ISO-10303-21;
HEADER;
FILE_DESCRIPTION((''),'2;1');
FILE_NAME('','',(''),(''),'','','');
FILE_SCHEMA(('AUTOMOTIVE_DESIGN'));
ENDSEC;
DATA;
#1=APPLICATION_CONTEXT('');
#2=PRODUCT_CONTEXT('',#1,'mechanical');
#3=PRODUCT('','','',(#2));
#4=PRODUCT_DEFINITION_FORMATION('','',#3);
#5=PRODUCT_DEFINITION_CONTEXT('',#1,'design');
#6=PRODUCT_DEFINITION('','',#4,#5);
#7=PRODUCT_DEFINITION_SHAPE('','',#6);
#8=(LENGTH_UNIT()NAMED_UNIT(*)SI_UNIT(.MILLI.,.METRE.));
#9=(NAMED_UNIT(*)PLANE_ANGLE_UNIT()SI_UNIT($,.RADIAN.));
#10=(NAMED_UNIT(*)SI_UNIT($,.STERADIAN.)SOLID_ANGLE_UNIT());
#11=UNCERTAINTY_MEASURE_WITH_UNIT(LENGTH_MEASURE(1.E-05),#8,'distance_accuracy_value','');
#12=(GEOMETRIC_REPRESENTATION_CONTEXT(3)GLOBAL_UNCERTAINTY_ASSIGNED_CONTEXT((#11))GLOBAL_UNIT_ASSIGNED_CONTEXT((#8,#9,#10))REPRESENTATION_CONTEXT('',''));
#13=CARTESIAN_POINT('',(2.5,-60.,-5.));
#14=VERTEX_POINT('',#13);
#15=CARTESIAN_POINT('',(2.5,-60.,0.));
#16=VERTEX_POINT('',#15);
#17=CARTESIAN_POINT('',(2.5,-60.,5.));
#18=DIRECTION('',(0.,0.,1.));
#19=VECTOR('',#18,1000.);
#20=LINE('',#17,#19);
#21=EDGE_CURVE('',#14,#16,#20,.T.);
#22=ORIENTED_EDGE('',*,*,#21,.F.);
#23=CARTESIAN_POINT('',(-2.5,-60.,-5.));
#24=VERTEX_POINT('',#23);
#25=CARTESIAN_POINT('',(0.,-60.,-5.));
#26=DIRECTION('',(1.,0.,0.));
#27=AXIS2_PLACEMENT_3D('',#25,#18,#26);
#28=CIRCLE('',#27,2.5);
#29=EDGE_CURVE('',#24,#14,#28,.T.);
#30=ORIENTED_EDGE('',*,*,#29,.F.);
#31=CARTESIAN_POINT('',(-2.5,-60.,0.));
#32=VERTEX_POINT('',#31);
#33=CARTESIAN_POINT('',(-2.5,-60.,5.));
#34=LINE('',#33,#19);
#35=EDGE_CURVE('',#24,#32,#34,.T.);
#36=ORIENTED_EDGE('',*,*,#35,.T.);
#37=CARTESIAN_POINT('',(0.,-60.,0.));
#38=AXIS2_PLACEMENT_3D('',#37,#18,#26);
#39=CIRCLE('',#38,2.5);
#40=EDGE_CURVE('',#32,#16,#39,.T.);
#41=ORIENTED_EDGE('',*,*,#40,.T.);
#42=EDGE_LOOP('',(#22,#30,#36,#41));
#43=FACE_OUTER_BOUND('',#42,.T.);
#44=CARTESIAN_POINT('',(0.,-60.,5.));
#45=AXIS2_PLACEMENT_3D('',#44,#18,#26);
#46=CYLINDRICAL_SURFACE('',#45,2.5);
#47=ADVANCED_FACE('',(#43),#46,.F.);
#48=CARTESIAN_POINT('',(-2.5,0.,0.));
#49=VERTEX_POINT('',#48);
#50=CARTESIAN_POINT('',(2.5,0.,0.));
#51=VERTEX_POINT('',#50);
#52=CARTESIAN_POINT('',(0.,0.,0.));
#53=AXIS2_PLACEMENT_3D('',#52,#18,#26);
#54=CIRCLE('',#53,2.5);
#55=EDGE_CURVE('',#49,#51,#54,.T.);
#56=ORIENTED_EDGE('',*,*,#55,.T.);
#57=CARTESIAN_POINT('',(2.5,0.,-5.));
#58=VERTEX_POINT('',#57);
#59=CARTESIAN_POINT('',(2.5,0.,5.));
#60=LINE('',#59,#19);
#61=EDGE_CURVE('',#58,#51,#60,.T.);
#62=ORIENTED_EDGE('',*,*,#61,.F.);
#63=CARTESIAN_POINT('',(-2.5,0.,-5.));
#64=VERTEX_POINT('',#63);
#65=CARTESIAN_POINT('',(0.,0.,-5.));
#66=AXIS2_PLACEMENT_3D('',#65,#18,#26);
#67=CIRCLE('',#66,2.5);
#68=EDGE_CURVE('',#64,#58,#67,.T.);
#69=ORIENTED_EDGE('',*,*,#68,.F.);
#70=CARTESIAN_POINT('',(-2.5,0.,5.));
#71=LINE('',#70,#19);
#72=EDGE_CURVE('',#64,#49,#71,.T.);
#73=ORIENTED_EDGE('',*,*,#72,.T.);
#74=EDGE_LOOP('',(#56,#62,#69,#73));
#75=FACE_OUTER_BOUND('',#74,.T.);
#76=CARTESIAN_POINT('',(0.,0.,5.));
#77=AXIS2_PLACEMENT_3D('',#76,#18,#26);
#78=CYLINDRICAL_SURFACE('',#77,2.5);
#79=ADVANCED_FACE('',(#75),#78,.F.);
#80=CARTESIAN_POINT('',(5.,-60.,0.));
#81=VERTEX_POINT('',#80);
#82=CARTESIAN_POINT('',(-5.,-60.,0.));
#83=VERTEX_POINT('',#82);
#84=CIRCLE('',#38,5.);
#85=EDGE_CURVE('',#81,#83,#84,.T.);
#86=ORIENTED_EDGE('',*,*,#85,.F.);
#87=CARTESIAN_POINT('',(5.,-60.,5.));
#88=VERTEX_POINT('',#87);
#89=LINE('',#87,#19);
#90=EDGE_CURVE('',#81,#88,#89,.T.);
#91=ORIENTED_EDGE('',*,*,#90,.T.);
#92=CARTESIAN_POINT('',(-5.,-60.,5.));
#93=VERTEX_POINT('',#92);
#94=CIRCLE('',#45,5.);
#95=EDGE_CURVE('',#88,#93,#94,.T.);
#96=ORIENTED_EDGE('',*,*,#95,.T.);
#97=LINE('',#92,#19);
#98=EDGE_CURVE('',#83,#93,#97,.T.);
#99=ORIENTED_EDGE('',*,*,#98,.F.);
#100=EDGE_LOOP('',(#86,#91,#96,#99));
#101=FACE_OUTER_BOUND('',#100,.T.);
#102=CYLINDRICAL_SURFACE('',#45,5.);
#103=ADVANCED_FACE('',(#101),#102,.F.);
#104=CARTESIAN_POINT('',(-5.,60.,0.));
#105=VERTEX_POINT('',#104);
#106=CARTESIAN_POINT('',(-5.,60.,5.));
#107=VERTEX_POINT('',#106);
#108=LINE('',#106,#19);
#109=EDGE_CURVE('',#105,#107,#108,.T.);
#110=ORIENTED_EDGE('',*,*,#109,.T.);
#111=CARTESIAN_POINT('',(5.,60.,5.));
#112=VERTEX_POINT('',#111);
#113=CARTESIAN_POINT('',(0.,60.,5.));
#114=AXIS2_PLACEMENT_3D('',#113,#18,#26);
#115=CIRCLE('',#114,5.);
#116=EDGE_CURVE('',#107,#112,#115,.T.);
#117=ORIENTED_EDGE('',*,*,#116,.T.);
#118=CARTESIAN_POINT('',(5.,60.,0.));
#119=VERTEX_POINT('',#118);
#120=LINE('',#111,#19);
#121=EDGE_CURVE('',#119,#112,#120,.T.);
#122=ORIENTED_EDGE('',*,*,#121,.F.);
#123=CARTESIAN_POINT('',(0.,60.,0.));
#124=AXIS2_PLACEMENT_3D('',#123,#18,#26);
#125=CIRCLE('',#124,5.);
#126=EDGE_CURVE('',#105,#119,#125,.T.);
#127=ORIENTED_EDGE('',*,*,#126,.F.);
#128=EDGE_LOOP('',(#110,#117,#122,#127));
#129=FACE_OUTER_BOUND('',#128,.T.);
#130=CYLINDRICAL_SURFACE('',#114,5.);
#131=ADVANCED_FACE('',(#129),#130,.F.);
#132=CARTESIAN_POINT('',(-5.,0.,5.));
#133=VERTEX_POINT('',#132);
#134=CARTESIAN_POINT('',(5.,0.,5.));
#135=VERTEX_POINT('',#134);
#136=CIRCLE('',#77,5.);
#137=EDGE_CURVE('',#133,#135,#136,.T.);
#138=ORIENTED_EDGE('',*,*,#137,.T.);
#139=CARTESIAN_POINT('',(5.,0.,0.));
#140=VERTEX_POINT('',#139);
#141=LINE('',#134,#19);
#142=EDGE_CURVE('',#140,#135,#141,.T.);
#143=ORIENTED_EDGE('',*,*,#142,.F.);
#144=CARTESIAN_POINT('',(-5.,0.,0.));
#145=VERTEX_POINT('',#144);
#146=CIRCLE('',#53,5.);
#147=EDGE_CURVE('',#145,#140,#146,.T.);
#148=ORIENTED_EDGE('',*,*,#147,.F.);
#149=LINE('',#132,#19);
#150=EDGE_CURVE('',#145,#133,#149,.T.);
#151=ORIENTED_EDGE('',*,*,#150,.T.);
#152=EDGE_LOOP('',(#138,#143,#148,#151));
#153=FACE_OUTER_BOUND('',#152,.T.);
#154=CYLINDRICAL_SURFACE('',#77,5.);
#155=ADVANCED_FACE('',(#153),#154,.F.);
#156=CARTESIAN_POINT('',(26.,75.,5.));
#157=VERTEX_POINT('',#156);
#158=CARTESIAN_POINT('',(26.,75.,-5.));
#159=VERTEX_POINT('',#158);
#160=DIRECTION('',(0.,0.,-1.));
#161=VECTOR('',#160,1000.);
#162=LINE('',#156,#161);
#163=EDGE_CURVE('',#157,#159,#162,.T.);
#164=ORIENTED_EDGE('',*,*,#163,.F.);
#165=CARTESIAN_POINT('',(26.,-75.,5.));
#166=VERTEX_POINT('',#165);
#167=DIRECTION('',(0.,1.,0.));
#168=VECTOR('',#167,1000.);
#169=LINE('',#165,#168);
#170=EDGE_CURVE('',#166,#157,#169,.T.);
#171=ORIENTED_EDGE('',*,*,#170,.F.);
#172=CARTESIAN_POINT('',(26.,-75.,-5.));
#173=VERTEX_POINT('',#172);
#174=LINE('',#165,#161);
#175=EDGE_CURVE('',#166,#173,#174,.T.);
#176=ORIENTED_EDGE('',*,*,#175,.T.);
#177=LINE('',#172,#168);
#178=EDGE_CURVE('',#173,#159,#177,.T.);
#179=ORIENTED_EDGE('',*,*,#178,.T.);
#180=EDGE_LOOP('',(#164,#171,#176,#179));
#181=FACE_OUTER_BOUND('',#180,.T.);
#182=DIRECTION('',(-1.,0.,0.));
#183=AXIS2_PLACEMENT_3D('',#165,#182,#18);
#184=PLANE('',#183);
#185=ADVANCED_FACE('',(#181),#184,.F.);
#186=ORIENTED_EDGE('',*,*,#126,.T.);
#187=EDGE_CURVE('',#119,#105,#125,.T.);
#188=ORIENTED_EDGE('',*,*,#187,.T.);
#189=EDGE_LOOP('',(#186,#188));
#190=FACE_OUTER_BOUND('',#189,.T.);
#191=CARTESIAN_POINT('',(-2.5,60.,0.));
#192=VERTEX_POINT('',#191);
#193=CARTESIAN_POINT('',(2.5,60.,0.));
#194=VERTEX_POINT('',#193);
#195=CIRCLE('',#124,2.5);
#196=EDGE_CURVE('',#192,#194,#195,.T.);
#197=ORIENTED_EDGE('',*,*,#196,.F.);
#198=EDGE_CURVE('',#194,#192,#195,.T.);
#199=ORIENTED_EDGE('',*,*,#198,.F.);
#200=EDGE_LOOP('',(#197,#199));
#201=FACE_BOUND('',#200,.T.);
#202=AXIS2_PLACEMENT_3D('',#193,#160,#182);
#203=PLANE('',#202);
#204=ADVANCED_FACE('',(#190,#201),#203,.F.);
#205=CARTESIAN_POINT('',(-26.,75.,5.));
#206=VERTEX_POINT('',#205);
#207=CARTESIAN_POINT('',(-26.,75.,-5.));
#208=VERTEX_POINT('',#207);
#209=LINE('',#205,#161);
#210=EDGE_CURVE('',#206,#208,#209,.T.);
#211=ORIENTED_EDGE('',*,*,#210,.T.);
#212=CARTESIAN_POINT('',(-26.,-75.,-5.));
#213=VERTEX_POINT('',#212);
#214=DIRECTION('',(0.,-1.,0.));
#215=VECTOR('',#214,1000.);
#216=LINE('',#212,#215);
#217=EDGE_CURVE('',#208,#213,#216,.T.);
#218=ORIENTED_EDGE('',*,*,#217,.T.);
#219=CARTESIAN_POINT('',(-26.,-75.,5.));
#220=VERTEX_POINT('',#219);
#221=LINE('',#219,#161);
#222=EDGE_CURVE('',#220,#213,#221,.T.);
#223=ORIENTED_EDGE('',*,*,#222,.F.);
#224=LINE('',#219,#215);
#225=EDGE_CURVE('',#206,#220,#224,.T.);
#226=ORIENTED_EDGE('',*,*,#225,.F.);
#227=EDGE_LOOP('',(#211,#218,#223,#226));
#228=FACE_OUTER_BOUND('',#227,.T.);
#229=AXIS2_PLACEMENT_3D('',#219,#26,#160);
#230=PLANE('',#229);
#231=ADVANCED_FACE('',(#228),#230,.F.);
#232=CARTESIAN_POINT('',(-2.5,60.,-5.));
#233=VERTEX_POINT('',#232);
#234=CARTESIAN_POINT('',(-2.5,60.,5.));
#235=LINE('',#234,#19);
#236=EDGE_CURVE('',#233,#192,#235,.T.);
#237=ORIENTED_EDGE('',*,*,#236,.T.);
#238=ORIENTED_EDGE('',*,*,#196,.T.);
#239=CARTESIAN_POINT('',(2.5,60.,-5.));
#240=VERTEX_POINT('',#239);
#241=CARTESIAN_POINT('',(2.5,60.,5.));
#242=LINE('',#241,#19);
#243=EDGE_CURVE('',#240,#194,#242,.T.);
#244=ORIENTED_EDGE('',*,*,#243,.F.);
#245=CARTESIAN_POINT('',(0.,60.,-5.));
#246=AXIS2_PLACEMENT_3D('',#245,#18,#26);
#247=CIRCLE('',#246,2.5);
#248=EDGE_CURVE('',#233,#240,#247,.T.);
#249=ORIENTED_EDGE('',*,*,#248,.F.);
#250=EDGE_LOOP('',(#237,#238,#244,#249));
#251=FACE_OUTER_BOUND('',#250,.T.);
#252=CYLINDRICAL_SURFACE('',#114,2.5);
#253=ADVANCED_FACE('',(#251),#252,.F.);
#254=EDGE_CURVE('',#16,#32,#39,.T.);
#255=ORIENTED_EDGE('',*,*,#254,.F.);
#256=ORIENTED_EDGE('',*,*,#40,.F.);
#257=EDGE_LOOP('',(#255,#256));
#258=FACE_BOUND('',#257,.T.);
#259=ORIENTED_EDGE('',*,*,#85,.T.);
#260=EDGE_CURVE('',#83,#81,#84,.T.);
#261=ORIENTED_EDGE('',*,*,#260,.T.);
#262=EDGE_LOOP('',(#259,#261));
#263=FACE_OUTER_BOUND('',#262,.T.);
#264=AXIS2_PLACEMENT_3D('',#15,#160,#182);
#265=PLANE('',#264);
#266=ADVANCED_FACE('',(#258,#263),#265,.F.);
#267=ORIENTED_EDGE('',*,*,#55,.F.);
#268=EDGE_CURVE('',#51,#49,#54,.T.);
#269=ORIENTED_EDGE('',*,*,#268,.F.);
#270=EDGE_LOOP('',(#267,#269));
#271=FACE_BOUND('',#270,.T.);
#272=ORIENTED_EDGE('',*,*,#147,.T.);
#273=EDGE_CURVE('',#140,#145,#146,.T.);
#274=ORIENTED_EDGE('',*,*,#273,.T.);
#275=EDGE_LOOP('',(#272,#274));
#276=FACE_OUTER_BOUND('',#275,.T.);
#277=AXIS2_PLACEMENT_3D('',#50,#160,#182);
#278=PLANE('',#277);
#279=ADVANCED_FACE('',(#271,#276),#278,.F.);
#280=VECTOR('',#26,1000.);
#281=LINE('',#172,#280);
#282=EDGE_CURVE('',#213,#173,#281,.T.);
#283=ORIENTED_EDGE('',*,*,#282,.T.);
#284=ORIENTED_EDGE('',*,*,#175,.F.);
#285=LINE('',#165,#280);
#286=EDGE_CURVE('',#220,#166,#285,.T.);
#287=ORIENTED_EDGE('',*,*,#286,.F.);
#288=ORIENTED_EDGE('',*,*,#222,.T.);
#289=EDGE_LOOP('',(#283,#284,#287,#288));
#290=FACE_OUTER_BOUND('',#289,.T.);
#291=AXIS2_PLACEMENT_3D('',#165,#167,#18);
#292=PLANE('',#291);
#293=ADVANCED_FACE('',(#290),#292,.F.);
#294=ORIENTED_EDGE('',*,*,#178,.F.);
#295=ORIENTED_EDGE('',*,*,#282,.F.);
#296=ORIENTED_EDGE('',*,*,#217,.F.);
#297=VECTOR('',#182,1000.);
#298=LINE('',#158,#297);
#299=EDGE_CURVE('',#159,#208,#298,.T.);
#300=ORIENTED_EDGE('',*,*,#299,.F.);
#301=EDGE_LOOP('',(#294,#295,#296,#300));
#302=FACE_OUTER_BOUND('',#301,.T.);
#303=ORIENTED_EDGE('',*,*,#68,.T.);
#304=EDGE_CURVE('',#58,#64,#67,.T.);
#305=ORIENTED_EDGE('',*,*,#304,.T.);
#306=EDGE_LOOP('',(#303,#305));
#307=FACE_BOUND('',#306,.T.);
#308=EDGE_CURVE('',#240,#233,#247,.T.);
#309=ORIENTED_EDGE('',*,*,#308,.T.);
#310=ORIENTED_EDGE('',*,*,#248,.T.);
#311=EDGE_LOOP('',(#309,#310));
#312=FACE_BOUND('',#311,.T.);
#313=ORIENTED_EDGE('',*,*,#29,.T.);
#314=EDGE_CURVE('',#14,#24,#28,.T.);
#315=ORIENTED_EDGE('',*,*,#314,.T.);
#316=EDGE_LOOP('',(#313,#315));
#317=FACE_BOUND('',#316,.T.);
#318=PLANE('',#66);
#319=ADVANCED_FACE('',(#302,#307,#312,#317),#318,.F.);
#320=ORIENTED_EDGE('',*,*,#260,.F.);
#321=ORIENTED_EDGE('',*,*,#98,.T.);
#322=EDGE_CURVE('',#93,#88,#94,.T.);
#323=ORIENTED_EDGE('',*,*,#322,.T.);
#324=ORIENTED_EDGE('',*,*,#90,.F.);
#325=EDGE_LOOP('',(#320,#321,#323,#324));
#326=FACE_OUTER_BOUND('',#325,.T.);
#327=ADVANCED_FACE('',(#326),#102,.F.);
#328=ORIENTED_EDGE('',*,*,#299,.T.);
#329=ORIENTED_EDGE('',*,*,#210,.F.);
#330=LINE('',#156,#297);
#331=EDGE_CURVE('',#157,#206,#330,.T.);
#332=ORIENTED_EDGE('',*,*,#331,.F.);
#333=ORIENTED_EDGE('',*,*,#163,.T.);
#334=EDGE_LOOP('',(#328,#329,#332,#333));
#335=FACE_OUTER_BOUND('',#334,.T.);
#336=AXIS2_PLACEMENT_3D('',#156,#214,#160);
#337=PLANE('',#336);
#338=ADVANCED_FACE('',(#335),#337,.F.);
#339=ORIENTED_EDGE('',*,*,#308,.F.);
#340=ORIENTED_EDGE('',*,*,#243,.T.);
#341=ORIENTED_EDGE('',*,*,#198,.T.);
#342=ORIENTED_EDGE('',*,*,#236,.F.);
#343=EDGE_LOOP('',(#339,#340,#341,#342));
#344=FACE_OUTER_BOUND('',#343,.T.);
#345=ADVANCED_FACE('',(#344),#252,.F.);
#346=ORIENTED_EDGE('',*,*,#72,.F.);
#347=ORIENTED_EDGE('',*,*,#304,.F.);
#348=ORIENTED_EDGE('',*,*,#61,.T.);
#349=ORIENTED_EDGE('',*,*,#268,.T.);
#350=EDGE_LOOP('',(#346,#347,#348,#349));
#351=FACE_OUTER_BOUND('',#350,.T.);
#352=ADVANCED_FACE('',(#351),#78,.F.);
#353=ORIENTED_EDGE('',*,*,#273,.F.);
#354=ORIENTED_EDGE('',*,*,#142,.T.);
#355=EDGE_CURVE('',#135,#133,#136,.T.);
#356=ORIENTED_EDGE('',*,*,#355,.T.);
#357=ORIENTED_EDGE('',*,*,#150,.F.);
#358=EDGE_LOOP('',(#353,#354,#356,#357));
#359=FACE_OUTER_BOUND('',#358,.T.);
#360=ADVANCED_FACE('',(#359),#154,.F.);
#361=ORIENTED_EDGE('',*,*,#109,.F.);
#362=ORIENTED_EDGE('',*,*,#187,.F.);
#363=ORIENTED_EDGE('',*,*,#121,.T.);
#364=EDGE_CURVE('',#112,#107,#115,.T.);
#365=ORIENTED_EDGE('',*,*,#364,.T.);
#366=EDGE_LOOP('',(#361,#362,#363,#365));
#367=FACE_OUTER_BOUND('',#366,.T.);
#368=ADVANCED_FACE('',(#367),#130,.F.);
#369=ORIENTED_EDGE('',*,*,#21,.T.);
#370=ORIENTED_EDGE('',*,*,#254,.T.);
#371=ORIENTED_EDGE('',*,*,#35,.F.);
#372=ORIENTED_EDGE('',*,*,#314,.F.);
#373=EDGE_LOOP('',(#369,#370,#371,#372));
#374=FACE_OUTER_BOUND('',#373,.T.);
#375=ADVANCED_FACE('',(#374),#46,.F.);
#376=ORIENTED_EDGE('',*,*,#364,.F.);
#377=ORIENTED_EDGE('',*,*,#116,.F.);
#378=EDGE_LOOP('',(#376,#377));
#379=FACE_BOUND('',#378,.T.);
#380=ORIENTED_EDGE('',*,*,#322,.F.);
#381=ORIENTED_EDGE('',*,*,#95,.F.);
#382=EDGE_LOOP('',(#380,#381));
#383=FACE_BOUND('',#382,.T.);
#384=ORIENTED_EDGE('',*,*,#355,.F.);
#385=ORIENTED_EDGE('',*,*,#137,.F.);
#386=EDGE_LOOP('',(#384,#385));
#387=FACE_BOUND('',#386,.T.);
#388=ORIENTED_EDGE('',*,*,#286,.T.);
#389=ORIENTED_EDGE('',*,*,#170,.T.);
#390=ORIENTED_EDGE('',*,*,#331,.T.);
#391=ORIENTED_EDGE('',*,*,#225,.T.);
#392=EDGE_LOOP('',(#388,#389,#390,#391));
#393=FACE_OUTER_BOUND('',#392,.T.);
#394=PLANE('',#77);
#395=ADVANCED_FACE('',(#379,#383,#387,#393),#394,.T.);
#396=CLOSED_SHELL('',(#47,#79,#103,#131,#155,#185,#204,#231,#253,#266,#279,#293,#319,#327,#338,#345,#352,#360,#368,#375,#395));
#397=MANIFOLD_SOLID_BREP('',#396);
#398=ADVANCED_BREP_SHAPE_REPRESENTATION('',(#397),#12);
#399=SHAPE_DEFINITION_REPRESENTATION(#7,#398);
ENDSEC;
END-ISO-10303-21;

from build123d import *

# Parameters (mm, degrees)
SKETCH1_W           = 52
SKETCH1_H           = 150
BOSS_EXTRUDE1_DEPTH = 5
HOLE1_D             = 5
HOLE1_CBORE_D       = 10
HOLE1_CBORE_DEPTH   = 5


with BuildPart() as part:
    # Sketch1 → Boss-Extrude1 (new, symmetric)
    with BuildSketch(Plane.XY):
        Rectangle(SKETCH1_W, SKETCH1_H)
    extrude(amount=BOSS_EXTRUDE1_DEPTH, both=True)

    # Hole1 (through all)
    with Locations(Plane.XY.offset(5)):
        with Locations((0, 60), (0, -60), (0, 0)):
            CounterBoreHole(HOLE1_D / 2, HOLE1_CBORE_D / 2, HOLE1_CBORE_DEPTH)


solid = part.part
